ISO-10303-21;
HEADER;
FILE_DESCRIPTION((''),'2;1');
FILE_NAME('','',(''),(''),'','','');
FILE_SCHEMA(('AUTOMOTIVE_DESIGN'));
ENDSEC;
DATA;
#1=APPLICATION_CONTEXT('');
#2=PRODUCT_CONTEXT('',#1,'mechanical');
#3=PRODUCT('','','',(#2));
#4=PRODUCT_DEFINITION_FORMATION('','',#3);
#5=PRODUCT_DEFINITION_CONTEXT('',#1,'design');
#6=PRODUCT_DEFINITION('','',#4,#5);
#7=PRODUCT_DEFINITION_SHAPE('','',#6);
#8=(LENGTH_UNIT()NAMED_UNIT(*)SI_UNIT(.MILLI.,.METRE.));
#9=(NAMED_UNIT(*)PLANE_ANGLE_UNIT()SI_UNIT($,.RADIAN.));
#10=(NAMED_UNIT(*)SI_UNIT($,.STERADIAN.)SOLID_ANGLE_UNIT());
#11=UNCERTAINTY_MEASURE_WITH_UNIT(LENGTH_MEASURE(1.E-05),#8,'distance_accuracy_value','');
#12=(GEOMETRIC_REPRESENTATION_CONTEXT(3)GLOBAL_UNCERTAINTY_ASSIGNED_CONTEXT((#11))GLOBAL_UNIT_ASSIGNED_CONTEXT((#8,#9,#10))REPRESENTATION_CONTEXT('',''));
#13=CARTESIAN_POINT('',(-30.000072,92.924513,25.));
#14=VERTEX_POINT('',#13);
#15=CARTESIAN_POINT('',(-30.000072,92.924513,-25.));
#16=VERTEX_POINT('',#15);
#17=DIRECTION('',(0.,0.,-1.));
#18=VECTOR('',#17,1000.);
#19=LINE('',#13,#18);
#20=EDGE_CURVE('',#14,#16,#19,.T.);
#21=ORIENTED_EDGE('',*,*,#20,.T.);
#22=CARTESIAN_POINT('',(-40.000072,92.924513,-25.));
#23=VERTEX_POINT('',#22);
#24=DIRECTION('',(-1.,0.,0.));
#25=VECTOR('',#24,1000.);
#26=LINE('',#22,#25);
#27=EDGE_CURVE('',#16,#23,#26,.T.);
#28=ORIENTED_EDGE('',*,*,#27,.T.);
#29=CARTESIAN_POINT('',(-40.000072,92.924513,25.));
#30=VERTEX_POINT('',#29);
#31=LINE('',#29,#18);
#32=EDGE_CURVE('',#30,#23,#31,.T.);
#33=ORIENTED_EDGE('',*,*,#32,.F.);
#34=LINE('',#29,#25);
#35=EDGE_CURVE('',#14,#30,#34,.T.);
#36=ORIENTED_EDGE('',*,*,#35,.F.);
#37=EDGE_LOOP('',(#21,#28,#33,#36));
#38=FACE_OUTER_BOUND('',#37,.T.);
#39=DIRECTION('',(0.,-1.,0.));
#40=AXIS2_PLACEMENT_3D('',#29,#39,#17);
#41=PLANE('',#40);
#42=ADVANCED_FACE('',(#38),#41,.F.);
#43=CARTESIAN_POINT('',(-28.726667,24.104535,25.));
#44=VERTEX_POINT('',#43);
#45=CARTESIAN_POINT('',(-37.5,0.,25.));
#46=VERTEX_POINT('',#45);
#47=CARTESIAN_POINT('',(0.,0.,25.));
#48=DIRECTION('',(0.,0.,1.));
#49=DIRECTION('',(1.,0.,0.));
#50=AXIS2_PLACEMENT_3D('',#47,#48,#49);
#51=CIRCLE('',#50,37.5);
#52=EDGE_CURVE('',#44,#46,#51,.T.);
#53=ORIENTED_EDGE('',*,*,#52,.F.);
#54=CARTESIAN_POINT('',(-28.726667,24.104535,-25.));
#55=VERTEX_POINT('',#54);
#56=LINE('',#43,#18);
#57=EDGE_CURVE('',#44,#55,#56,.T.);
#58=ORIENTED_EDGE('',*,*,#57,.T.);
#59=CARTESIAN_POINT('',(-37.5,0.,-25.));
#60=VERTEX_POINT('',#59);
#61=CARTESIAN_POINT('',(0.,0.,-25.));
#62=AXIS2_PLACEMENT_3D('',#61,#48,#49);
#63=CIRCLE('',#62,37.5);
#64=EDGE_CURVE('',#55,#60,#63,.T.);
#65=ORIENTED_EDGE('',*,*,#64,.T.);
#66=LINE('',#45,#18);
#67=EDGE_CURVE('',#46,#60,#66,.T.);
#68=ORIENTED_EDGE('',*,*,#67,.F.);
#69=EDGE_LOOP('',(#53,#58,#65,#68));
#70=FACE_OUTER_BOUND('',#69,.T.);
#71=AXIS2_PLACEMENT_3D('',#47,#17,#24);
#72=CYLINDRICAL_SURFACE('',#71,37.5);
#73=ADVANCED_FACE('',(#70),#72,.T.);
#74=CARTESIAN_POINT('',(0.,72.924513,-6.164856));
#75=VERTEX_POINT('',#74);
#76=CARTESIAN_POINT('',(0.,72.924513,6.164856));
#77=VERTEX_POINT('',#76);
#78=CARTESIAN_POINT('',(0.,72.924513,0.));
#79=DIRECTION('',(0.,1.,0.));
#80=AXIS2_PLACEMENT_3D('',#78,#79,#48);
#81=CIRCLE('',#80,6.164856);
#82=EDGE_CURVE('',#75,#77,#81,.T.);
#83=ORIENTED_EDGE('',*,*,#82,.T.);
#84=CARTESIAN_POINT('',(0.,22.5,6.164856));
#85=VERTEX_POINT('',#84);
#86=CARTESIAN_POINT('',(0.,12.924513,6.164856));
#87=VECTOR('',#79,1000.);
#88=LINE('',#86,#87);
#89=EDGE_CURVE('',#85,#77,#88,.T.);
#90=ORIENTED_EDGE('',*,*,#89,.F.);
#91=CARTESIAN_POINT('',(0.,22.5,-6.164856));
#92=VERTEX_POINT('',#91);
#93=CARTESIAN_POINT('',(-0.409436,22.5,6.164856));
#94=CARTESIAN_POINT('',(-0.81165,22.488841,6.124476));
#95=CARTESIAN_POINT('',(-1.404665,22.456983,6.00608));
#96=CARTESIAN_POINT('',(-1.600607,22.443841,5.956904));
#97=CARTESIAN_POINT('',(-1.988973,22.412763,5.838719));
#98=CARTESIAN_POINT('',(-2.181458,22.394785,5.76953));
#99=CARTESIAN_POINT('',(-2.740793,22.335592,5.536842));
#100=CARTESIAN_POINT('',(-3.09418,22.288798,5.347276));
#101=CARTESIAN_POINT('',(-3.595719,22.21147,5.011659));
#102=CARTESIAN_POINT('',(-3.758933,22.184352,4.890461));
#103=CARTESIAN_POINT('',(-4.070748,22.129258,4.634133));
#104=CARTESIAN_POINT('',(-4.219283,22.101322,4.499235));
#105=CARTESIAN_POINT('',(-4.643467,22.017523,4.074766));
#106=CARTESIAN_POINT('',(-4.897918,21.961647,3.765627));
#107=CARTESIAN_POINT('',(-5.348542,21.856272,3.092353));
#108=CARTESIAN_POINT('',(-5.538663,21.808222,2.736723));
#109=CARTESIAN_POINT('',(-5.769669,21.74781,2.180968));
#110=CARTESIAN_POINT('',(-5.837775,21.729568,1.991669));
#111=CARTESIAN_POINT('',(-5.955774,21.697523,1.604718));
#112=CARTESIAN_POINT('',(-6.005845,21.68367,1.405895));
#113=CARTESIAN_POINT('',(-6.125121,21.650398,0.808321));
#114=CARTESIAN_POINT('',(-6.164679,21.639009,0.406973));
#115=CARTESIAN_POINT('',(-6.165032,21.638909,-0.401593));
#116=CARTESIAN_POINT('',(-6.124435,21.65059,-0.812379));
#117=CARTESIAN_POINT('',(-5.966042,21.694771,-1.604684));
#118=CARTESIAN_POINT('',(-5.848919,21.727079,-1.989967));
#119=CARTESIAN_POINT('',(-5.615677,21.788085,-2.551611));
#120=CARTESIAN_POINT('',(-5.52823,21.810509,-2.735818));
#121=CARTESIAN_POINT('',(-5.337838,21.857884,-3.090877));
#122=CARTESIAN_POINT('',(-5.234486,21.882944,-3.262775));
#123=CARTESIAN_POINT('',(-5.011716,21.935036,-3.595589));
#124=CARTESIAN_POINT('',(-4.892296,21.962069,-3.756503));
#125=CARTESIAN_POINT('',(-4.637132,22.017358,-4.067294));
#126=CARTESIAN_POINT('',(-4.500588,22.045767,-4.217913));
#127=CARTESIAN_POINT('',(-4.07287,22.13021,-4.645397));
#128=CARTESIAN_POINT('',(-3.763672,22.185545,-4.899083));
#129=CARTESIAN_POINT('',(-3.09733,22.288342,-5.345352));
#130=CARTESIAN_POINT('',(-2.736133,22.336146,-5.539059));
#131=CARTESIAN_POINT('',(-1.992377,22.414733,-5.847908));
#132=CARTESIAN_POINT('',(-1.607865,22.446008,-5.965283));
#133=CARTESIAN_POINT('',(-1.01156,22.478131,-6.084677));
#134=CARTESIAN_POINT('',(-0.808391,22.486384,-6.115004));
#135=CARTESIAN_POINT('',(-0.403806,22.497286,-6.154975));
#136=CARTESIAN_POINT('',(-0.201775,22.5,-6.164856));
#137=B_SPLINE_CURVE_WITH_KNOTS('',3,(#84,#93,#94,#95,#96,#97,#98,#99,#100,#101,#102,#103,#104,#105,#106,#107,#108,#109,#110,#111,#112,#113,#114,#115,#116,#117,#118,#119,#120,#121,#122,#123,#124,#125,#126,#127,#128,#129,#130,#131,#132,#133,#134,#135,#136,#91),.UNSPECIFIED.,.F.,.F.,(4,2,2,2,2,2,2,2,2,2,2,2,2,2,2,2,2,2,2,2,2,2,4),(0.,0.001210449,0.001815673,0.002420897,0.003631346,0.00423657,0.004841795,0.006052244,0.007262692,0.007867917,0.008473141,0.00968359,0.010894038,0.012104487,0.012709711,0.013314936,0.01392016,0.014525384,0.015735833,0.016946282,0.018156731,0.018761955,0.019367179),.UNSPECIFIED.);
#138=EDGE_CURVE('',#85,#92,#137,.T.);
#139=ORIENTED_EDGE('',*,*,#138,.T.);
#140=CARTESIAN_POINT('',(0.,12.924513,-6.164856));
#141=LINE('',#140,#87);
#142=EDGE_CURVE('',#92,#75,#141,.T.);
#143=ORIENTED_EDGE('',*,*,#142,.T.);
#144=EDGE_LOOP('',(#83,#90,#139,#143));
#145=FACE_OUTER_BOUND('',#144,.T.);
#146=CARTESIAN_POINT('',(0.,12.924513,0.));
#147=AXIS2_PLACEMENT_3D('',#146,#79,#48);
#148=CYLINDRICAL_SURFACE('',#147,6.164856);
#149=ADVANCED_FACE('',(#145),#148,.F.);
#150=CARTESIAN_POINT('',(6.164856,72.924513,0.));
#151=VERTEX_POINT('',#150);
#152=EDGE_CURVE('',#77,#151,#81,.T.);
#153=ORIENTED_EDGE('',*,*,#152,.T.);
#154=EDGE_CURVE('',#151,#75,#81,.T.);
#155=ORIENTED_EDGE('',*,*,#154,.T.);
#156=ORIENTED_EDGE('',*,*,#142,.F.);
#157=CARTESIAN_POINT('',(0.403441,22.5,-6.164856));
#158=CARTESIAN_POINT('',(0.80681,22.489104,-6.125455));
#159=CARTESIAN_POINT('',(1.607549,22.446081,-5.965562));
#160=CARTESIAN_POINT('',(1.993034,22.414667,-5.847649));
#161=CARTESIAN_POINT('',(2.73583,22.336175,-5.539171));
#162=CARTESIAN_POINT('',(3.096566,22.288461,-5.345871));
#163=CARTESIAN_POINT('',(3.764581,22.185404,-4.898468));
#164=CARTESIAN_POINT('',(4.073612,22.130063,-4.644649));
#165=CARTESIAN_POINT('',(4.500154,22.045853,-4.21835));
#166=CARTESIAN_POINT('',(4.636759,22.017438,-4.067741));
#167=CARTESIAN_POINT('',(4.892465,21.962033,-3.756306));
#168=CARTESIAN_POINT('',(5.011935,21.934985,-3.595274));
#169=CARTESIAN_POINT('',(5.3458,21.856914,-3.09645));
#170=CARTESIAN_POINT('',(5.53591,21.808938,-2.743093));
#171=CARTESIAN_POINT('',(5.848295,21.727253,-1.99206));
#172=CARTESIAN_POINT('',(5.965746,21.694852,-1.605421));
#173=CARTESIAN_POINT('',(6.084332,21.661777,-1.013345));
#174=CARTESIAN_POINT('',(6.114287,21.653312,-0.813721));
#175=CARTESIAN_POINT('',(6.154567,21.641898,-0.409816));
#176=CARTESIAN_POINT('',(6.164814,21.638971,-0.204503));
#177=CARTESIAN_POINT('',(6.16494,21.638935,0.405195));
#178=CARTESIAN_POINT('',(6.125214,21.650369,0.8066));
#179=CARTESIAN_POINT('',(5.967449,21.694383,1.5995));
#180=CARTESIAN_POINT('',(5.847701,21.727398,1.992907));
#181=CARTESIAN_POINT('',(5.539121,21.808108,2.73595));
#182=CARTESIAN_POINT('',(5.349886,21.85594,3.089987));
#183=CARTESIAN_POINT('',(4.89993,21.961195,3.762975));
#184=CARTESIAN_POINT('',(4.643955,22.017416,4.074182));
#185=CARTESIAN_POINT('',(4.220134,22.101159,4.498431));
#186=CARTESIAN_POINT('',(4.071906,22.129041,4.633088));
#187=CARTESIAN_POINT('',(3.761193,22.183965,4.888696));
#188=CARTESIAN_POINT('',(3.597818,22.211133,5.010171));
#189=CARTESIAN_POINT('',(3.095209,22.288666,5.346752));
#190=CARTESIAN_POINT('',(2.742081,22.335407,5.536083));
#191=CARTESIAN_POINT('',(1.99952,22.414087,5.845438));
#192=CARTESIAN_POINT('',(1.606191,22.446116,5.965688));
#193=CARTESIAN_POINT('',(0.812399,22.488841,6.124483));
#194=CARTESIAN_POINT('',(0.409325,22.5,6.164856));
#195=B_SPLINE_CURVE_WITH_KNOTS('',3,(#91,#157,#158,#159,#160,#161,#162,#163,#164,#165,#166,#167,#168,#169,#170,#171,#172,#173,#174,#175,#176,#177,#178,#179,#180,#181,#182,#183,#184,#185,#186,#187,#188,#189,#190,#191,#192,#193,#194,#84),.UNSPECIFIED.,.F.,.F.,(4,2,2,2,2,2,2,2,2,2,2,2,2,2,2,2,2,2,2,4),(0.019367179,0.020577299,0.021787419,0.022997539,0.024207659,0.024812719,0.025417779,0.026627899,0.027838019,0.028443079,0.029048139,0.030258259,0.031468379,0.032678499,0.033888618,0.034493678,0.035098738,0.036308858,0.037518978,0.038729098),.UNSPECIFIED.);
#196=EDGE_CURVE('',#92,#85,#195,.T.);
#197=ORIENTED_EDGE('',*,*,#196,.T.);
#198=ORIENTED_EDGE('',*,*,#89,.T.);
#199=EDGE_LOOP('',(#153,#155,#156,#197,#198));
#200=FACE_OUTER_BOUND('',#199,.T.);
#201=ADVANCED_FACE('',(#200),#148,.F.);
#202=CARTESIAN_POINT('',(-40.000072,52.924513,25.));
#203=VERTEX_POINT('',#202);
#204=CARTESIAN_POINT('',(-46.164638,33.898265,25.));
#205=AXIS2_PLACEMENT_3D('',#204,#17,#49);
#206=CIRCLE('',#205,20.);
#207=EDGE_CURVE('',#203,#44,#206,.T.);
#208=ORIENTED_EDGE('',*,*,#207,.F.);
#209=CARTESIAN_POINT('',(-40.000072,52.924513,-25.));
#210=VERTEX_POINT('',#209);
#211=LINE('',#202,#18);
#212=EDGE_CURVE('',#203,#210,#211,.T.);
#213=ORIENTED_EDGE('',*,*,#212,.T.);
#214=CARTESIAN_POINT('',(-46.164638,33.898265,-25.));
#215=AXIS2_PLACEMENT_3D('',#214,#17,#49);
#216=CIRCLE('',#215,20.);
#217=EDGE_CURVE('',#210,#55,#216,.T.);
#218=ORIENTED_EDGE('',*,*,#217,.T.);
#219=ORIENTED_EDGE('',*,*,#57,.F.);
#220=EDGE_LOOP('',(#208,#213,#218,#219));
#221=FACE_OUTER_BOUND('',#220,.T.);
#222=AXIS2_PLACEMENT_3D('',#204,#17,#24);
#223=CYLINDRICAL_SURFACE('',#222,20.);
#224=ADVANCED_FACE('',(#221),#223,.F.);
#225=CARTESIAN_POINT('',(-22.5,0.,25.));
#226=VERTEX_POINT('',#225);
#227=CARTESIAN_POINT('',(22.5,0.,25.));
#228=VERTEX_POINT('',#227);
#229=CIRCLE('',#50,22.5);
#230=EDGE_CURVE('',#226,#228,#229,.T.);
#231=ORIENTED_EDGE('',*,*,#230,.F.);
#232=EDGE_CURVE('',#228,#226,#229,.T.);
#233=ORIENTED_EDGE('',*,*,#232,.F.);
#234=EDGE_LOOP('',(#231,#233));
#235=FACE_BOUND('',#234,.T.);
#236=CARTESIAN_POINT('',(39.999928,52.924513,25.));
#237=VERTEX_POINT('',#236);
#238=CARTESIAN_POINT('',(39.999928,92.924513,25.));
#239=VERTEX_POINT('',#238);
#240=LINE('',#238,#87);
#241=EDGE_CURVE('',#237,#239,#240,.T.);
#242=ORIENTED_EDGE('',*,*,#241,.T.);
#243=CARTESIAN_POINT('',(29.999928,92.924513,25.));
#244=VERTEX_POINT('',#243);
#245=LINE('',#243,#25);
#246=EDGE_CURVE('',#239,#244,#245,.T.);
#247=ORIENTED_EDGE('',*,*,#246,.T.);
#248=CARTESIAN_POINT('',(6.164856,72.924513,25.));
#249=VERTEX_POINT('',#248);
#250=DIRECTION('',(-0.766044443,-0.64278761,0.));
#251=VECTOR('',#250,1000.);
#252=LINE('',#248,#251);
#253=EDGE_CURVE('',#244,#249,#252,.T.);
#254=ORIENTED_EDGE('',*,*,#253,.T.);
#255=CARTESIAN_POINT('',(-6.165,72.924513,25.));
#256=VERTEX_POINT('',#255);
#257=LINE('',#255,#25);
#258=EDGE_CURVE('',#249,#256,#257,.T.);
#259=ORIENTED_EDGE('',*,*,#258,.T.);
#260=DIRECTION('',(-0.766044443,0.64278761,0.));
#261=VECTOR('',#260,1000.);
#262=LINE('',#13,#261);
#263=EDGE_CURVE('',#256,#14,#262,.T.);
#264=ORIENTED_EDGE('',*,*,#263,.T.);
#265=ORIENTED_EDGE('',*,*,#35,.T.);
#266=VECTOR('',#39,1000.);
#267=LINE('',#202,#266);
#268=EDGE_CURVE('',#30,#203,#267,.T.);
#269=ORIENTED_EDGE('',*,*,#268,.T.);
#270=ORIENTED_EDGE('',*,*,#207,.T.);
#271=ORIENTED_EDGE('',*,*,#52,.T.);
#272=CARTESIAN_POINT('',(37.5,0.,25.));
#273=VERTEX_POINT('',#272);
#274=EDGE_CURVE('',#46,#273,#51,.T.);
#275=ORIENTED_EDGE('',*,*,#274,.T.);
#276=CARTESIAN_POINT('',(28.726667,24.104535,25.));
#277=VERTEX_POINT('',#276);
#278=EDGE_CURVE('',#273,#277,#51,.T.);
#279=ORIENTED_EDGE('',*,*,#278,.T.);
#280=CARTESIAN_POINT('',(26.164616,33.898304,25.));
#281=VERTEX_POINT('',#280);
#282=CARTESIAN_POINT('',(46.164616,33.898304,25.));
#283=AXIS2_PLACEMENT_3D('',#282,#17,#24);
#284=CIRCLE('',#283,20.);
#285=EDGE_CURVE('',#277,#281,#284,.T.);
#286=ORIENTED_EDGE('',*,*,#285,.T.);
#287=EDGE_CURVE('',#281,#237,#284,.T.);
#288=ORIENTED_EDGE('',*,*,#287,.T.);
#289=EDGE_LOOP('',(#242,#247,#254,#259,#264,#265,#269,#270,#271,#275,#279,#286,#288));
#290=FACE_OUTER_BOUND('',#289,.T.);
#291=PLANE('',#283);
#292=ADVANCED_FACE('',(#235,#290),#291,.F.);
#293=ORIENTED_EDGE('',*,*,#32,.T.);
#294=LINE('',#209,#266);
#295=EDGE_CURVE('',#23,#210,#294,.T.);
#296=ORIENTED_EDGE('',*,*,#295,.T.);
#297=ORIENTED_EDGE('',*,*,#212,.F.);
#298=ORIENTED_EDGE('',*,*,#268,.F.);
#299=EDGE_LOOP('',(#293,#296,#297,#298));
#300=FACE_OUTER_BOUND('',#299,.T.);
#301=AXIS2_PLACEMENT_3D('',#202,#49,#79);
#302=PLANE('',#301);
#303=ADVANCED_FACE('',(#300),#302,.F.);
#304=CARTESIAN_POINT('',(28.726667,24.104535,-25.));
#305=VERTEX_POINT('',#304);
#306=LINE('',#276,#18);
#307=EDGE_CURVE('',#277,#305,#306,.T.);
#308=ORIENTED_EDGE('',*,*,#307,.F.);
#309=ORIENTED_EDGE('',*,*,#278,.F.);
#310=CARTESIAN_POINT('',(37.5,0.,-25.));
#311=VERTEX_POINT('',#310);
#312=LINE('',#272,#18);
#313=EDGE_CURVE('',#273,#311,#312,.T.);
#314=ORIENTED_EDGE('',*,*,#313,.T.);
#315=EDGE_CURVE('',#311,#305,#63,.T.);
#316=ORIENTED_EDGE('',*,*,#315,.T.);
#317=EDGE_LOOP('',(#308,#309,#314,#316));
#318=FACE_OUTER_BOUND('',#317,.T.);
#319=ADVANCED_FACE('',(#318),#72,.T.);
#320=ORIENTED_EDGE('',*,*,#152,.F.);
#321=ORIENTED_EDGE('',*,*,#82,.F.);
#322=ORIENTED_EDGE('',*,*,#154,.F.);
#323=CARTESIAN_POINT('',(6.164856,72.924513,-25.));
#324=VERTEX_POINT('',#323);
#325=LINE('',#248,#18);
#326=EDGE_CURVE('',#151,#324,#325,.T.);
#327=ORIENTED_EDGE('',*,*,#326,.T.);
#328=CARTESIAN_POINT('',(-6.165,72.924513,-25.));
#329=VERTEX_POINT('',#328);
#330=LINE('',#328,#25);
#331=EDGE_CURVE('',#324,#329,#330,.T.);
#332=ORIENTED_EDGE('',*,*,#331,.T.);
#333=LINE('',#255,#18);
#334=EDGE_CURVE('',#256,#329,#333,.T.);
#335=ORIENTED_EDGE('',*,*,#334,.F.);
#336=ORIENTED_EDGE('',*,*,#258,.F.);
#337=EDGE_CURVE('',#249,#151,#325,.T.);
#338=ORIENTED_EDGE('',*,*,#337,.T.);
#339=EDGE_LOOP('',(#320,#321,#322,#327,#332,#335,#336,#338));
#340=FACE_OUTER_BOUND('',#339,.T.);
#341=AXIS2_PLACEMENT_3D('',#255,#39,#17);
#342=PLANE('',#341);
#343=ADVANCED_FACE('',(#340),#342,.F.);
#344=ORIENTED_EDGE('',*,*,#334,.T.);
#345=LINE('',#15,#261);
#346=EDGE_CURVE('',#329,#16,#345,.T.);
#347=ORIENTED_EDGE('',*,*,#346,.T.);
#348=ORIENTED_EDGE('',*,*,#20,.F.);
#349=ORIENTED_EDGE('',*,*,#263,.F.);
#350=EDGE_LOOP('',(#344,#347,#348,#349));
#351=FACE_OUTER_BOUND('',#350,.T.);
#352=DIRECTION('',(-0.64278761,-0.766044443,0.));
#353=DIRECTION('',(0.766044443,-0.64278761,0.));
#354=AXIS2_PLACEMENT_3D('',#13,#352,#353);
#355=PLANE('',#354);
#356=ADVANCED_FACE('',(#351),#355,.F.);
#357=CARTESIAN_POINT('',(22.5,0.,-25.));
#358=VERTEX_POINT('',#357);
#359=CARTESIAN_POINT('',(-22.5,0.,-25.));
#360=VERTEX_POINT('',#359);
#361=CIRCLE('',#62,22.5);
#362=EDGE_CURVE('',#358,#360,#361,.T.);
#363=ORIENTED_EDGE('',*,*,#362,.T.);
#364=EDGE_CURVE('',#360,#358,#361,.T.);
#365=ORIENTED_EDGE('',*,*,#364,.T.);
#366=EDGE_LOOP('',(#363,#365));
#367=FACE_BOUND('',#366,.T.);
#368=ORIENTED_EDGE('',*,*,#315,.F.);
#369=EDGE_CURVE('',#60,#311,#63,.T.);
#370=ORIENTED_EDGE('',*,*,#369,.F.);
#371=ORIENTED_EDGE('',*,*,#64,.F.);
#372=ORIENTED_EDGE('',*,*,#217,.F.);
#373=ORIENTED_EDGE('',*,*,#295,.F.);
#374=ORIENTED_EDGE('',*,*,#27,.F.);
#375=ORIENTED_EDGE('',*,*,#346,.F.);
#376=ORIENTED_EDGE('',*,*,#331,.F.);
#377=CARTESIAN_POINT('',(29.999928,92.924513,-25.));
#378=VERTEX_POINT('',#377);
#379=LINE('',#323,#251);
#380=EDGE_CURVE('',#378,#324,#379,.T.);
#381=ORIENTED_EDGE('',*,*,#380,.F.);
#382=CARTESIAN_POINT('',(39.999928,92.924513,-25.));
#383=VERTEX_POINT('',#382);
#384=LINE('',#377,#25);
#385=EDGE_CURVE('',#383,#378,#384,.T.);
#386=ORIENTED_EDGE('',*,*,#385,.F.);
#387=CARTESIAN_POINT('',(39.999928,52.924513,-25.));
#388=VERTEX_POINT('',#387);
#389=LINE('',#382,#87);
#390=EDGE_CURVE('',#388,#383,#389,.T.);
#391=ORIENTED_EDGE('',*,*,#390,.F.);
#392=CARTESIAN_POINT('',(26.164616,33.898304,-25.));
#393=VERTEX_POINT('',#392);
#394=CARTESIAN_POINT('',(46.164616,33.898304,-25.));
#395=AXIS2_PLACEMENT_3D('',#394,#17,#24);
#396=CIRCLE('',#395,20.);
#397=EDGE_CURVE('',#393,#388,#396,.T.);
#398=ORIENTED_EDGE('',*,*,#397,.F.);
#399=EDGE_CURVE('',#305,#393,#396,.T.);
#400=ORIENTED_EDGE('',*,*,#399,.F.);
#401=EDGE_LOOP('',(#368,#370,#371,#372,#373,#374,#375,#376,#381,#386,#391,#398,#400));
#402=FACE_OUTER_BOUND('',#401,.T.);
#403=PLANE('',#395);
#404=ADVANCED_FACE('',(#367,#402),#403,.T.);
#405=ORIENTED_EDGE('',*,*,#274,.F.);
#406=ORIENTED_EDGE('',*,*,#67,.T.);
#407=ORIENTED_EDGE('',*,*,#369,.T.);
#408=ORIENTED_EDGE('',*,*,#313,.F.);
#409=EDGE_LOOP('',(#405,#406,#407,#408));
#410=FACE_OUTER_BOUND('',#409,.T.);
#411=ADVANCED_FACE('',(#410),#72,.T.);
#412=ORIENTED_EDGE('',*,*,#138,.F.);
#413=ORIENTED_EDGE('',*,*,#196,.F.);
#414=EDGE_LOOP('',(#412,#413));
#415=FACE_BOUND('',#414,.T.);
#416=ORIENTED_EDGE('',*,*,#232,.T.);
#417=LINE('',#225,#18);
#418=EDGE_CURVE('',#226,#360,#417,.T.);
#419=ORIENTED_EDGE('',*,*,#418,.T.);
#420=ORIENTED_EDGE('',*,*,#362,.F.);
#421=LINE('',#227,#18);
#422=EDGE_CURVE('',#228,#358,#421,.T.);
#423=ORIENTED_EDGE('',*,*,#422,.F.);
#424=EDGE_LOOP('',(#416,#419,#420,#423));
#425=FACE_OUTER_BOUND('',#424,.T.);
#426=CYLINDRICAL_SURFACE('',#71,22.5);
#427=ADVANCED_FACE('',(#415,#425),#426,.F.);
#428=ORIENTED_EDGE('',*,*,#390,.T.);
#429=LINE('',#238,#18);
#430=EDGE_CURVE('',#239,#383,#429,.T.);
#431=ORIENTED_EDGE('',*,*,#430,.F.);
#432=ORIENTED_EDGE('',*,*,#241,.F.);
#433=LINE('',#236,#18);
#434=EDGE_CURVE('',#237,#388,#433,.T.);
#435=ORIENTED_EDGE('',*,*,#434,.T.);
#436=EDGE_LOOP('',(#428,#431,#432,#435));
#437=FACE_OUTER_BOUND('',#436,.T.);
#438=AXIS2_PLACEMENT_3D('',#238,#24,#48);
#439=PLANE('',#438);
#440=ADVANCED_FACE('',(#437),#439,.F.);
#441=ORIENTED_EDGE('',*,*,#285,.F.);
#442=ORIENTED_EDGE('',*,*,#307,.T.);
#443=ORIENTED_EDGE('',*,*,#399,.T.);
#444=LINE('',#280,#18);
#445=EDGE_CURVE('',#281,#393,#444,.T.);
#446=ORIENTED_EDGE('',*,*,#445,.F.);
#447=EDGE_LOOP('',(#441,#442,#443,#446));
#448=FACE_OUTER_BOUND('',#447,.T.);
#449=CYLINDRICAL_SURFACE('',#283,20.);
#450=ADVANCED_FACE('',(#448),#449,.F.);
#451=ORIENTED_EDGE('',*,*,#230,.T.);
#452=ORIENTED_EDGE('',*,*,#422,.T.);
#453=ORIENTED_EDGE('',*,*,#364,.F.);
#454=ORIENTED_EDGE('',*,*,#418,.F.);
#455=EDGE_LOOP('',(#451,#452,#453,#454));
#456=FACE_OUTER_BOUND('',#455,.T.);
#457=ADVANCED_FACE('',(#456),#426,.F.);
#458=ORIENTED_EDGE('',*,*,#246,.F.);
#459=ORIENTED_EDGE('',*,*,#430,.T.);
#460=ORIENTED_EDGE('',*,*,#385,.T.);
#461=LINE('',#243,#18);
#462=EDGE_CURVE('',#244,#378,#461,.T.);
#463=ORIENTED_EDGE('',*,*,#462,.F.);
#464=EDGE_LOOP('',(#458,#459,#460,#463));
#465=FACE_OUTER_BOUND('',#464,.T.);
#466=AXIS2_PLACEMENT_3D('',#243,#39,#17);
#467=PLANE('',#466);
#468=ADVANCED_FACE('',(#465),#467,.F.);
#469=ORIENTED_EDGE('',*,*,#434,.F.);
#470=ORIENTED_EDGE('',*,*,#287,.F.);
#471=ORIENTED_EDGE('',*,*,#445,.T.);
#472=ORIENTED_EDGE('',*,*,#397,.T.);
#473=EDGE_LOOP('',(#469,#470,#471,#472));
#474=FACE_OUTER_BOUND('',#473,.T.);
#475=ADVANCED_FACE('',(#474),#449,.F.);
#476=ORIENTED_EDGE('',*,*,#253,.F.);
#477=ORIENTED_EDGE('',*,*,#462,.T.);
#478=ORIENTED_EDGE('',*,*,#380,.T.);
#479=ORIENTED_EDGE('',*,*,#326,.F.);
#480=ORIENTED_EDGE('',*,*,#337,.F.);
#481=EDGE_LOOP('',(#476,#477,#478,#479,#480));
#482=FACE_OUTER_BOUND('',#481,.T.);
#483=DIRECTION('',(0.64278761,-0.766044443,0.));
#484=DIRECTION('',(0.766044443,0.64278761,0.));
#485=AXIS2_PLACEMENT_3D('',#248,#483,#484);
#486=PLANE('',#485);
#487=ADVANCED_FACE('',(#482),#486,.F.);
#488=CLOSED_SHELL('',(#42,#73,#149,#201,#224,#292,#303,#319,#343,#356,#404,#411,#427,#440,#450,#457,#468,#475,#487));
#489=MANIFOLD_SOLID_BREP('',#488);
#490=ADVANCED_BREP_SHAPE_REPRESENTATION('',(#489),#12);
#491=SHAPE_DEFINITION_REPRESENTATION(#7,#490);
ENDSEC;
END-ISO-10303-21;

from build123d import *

# Parameters (mm, degrees)
V_BLOCK_PROFILE_SKETCH_R = 22.5
V_BLOCK_BODY_DEPTH       = 25
CROSS_HOLE_SKETCH_R      = 6.164856296
CROSS_HOLE_DEPTH         = 60


with BuildPart() as part:
    # V-Block Profile Sketch → V-Block Body (new, symmetric)
    with BuildSketch(Plane.XY):
        with BuildLine():
            Line((-40.000071852, 52.924513188), (-40.000071852, 92.924513188))
            Line((-40.000071852, 92.924513188), (-30.000071852, 92.924513188))
            Line((-30.000071852, 92.924513188), (-6.165, 72.924513188))
            Line((-6.165, 72.924513188), (6.164856296, 72.924513188))
            Line((6.164856296, 72.924513188), (29.999928148, 92.924513188))
            Line((29.999928148, 92.924513188), (39.999928148, 92.924513188))
            Line((39.999928148, 92.924513188), (39.999928148, 52.924513188))
            ThreePointArc((39.999928148, 52.924513188), (27.538857009, 41.183981608), (28.726666617, 24.104535363))
            ThreePointArc((28.726666617, 24.104535363), (0, -37.5), (-28.726666617, 24.104535363))
            ThreePointArc((-28.726666617, 24.104535363), (-27.538910641, 41.184022764), (-40.000071852, 52.924513188))
        make_face()
        Circle(V_BLOCK_PROFILE_SKETCH_R, mode=Mode.SUBTRACT)
    extrude(amount=V_BLOCK_BODY_DEPTH, both=True)

    # Cross Hole Sketch → Cross Hole (cut)
    with BuildSketch(Plane(origin=(0, 72.924513188, 0), x_dir=(1, 0, 0), z_dir=(0, 1, 0))):
        with Locations(Location((0, 0, 0), (0, 0, 270))):
            Circle(CROSS_HOLE_SKETCH_R)
    extrude(amount=-CROSS_HOLE_DEPTH, mode=Mode.SUBTRACT)


solid = part.part
